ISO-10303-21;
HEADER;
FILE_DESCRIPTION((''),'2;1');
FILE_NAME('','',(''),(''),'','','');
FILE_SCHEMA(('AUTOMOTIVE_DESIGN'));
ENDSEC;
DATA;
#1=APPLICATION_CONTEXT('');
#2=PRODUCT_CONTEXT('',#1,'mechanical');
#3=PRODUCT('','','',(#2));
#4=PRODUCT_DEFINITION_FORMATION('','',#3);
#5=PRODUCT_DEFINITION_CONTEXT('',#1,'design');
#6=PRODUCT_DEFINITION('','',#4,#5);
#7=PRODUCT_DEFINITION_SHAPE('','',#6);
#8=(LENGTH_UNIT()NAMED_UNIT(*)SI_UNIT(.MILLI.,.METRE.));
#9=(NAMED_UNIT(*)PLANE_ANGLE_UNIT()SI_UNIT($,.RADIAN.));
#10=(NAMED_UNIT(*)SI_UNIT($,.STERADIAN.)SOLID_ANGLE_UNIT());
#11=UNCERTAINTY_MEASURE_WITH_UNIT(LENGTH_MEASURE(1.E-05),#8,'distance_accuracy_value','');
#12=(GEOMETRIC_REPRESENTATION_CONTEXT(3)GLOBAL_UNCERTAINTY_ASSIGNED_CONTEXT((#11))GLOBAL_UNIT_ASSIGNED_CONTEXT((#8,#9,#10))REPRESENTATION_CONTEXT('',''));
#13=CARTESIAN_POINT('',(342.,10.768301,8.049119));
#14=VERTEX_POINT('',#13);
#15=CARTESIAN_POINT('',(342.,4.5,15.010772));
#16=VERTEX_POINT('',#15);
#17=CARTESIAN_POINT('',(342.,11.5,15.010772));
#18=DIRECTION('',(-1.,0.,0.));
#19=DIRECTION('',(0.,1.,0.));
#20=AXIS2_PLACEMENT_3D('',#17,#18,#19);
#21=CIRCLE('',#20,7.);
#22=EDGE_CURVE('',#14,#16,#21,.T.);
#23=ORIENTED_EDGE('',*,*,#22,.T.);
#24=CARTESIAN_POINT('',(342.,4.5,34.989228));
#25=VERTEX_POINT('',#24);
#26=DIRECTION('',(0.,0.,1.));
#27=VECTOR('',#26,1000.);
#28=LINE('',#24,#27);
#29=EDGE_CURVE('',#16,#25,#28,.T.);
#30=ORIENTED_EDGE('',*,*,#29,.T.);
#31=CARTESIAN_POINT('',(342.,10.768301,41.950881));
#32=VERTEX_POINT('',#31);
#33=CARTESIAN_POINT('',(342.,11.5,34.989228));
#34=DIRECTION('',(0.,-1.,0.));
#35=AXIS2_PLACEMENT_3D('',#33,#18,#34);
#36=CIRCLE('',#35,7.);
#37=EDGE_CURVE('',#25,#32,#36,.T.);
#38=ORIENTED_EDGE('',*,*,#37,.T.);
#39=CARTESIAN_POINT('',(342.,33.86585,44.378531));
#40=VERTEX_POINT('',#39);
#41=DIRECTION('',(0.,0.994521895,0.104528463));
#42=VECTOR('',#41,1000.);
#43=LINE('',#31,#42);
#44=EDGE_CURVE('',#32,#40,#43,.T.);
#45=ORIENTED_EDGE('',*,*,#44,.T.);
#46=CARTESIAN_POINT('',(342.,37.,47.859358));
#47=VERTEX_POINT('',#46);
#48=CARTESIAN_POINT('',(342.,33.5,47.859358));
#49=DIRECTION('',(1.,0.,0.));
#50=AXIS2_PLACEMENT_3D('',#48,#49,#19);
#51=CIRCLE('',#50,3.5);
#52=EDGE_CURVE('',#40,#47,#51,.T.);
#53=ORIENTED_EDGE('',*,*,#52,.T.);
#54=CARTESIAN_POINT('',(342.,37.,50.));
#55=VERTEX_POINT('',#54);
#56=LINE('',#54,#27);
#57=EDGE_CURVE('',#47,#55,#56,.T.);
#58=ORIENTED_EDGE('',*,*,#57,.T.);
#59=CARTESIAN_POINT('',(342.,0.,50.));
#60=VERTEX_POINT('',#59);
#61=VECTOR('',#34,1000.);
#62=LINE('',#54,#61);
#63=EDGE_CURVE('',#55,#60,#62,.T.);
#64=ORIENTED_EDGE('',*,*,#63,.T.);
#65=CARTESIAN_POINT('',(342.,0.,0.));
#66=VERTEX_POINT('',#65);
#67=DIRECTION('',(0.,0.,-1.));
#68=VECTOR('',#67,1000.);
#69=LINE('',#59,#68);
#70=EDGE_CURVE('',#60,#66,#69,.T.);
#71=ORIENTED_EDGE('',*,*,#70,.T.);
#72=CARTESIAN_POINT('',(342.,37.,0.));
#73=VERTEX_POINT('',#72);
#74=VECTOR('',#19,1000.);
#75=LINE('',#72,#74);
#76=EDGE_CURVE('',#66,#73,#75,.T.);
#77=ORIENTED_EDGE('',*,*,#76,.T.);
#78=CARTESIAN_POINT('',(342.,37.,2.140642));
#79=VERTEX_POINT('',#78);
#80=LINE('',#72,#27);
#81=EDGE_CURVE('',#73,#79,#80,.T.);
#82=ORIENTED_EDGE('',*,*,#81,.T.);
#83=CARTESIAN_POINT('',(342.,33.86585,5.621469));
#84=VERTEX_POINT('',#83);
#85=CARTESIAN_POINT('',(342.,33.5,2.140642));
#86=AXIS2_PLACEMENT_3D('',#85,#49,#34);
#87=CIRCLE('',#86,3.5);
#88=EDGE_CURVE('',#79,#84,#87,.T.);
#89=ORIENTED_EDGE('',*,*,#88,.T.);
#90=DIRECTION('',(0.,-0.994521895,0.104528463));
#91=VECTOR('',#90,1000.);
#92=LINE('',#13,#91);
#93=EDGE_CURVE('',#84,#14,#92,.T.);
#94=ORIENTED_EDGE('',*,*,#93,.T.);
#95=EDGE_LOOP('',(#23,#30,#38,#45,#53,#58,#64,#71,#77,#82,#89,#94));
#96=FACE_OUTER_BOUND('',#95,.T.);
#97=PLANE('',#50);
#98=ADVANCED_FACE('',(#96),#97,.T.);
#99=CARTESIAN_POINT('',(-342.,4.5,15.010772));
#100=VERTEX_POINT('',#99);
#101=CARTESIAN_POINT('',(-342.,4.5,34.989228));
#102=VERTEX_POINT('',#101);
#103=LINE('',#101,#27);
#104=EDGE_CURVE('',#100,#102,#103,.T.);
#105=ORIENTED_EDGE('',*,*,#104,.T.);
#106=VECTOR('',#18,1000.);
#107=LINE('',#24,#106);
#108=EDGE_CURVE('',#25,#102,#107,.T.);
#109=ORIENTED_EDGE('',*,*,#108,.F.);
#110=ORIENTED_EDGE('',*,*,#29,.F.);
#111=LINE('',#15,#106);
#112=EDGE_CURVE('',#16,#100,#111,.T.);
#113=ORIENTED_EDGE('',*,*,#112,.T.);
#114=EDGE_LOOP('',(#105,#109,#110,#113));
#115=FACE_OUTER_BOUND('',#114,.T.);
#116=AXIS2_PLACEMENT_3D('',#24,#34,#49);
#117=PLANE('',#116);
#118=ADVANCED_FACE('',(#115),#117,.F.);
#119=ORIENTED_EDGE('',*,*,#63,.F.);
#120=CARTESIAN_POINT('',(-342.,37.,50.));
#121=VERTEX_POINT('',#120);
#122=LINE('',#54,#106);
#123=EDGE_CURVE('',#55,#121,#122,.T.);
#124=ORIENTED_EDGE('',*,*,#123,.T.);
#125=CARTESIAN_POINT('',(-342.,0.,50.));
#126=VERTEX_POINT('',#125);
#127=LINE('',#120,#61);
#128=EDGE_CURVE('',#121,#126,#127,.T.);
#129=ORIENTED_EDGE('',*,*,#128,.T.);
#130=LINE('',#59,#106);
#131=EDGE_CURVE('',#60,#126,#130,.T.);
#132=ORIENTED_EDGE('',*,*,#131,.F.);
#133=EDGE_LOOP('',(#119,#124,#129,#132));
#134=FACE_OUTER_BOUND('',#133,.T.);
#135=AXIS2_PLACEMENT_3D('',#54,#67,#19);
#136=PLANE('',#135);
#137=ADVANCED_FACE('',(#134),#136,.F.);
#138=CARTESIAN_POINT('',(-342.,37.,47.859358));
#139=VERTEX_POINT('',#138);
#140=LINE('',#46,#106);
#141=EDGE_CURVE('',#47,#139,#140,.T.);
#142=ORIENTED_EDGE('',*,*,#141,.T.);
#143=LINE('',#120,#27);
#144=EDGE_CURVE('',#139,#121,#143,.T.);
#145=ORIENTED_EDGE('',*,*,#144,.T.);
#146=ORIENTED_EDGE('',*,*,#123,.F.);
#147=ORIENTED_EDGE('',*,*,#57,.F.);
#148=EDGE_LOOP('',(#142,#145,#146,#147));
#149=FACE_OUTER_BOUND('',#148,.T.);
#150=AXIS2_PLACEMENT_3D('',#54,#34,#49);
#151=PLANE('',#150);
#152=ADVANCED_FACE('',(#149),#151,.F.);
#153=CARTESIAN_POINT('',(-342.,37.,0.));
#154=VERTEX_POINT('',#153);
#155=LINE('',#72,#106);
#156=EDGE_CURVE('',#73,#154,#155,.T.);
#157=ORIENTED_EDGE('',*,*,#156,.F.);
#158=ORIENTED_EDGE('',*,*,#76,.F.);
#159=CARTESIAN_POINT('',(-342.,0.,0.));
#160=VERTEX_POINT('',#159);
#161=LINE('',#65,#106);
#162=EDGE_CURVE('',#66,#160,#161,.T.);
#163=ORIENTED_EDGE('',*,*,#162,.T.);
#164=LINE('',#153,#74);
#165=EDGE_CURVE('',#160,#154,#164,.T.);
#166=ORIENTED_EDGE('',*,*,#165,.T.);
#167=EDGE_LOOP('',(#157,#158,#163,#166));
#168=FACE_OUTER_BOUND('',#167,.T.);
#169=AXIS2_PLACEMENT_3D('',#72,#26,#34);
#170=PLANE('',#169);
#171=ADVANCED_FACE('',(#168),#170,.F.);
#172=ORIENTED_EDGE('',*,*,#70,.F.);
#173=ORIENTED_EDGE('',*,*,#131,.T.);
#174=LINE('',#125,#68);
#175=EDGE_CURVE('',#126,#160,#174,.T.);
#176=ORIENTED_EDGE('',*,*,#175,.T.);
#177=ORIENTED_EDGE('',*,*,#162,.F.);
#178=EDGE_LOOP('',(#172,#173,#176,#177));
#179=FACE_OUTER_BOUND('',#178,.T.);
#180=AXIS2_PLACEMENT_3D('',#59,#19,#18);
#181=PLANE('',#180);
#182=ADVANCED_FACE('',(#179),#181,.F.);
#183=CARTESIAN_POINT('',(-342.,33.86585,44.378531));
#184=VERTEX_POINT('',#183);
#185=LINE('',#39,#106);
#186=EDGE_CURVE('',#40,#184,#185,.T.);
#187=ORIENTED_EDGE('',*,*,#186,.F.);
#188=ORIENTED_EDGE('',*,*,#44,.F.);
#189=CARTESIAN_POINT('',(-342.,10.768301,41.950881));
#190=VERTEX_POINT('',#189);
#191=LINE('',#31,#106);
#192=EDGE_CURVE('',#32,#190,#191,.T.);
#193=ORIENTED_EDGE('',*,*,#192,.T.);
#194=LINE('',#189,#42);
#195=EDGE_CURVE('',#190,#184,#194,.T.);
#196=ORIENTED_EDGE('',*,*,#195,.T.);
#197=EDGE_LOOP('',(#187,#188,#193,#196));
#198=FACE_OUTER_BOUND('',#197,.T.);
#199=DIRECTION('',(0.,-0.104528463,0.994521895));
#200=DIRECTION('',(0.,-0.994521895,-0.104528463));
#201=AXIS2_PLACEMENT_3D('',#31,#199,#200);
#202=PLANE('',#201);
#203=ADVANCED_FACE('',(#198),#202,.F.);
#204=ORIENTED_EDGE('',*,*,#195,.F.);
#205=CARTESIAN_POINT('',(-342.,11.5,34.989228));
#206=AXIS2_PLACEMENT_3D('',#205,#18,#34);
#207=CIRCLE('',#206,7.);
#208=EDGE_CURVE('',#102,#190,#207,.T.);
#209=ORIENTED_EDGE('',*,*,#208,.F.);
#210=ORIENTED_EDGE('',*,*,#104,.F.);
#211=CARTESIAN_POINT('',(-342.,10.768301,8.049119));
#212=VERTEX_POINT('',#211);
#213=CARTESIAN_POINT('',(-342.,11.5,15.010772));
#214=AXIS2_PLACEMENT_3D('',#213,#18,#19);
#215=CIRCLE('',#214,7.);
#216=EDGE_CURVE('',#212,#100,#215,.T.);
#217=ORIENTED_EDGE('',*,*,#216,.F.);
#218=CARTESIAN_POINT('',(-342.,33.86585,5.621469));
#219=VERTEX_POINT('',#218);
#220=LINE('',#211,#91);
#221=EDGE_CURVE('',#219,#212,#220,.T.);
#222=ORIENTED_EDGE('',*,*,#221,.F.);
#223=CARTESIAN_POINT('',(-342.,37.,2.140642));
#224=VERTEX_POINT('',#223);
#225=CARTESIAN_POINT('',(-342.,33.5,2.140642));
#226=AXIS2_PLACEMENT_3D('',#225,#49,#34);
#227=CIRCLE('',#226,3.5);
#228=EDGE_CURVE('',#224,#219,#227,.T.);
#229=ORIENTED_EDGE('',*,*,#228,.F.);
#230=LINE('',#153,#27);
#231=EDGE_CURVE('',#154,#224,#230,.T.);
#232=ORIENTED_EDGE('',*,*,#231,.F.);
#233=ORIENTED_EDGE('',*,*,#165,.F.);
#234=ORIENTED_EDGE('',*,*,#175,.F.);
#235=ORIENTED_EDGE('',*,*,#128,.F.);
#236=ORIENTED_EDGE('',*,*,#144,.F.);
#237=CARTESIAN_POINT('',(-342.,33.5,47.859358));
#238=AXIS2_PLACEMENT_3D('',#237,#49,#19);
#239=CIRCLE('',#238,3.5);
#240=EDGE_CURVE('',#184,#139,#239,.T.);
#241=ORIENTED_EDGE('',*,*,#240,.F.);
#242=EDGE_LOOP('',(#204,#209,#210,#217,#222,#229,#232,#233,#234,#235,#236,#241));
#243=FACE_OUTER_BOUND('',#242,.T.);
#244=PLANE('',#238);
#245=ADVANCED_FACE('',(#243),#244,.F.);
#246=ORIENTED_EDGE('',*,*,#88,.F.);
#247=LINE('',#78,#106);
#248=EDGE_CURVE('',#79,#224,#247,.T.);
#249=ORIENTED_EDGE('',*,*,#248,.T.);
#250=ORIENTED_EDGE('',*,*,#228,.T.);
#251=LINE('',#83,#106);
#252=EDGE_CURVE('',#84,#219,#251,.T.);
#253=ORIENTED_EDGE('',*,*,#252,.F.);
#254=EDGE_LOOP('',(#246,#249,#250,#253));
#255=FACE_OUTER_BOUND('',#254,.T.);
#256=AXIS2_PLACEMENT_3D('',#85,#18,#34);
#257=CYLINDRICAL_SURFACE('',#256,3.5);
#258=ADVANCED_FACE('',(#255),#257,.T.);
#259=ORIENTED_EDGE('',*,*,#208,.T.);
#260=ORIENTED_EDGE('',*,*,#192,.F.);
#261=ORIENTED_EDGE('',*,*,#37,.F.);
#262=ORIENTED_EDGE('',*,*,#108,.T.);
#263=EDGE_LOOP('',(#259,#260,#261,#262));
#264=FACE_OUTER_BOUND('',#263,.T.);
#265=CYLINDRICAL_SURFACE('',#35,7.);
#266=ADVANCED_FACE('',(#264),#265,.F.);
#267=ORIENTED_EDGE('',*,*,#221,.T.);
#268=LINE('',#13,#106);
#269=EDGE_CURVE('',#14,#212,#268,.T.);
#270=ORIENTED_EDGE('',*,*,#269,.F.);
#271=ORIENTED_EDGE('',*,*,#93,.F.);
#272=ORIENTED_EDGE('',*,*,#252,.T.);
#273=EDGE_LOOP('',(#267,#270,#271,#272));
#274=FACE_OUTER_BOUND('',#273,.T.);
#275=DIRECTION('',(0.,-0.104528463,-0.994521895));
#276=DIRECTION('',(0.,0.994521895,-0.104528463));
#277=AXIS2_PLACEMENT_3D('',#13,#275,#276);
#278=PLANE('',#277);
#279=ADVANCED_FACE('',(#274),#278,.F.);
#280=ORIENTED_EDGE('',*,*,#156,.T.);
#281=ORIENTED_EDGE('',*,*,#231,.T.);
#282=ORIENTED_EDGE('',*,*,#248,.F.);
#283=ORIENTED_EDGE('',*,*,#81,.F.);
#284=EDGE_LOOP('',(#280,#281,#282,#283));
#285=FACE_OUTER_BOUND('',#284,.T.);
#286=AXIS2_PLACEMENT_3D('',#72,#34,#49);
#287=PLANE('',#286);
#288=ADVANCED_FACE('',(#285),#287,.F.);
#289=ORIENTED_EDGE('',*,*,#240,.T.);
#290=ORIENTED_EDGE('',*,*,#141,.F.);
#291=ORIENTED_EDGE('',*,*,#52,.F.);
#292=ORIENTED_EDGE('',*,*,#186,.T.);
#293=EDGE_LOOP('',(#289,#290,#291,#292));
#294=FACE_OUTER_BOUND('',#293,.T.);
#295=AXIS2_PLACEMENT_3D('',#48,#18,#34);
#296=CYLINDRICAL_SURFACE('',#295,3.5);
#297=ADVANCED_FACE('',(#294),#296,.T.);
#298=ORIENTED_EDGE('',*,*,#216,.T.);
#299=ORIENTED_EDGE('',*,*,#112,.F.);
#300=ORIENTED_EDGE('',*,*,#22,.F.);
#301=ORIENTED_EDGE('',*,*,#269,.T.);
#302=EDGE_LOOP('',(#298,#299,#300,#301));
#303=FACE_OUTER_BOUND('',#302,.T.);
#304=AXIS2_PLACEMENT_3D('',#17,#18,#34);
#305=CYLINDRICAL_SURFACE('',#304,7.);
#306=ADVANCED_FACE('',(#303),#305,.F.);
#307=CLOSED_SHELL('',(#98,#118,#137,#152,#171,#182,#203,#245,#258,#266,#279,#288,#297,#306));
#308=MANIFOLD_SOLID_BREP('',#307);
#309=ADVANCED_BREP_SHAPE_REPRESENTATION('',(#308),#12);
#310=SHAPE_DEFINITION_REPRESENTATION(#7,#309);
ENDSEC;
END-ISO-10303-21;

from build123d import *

# Parameters (mm, degrees)
GB_T_707_1988_HOT_ROLLED_CHANNEL_05_1_DEPTH = 684


with BuildPart() as part:
    # Sketch1 → GB/T 707-1988 hot-rolled channel 05(1) (new body)
    with BuildSketch(Plane.YZ.offset(-342)):
        with BuildLine():
            Line((37, 50), (0, 50))
            Line((0, 50), (0, 0))
            Line((0, 0), (37, 0))
            Line((37, 0), (37, 2.140642022))
            ThreePointArc((37, 2.140642022), (36.101006889, 4.482599144), (33.865849621, 5.621468656))
            Line((33.865849621, 5.621468656), (10.768300757, 8.049118866))
            ThreePointArc((10.768300757, 8.049118866), (6.297986222, 10.326857889), (4.5, 15.010772133))
            Line((4.5, 15.010772133), (4.5, 34.989227867))
            ThreePointArc((4.5, 34.989227867), (6.297986222, 39.673142111), (10.768300757, 41.950881134))
            Line((10.768300757, 41.950881134), (33.865849621, 44.378531344))
            ThreePointArc((33.865849621, 44.378531344), (36.101006889, 45.517400856), (37, 47.859357978))
            Line((37, 47.859357978), (37, 50))
        make_face()
    extrude(amount=GB_T_707_1988_HOT_ROLLED_CHANNEL_05_1_DEPTH)


solid = part.part
